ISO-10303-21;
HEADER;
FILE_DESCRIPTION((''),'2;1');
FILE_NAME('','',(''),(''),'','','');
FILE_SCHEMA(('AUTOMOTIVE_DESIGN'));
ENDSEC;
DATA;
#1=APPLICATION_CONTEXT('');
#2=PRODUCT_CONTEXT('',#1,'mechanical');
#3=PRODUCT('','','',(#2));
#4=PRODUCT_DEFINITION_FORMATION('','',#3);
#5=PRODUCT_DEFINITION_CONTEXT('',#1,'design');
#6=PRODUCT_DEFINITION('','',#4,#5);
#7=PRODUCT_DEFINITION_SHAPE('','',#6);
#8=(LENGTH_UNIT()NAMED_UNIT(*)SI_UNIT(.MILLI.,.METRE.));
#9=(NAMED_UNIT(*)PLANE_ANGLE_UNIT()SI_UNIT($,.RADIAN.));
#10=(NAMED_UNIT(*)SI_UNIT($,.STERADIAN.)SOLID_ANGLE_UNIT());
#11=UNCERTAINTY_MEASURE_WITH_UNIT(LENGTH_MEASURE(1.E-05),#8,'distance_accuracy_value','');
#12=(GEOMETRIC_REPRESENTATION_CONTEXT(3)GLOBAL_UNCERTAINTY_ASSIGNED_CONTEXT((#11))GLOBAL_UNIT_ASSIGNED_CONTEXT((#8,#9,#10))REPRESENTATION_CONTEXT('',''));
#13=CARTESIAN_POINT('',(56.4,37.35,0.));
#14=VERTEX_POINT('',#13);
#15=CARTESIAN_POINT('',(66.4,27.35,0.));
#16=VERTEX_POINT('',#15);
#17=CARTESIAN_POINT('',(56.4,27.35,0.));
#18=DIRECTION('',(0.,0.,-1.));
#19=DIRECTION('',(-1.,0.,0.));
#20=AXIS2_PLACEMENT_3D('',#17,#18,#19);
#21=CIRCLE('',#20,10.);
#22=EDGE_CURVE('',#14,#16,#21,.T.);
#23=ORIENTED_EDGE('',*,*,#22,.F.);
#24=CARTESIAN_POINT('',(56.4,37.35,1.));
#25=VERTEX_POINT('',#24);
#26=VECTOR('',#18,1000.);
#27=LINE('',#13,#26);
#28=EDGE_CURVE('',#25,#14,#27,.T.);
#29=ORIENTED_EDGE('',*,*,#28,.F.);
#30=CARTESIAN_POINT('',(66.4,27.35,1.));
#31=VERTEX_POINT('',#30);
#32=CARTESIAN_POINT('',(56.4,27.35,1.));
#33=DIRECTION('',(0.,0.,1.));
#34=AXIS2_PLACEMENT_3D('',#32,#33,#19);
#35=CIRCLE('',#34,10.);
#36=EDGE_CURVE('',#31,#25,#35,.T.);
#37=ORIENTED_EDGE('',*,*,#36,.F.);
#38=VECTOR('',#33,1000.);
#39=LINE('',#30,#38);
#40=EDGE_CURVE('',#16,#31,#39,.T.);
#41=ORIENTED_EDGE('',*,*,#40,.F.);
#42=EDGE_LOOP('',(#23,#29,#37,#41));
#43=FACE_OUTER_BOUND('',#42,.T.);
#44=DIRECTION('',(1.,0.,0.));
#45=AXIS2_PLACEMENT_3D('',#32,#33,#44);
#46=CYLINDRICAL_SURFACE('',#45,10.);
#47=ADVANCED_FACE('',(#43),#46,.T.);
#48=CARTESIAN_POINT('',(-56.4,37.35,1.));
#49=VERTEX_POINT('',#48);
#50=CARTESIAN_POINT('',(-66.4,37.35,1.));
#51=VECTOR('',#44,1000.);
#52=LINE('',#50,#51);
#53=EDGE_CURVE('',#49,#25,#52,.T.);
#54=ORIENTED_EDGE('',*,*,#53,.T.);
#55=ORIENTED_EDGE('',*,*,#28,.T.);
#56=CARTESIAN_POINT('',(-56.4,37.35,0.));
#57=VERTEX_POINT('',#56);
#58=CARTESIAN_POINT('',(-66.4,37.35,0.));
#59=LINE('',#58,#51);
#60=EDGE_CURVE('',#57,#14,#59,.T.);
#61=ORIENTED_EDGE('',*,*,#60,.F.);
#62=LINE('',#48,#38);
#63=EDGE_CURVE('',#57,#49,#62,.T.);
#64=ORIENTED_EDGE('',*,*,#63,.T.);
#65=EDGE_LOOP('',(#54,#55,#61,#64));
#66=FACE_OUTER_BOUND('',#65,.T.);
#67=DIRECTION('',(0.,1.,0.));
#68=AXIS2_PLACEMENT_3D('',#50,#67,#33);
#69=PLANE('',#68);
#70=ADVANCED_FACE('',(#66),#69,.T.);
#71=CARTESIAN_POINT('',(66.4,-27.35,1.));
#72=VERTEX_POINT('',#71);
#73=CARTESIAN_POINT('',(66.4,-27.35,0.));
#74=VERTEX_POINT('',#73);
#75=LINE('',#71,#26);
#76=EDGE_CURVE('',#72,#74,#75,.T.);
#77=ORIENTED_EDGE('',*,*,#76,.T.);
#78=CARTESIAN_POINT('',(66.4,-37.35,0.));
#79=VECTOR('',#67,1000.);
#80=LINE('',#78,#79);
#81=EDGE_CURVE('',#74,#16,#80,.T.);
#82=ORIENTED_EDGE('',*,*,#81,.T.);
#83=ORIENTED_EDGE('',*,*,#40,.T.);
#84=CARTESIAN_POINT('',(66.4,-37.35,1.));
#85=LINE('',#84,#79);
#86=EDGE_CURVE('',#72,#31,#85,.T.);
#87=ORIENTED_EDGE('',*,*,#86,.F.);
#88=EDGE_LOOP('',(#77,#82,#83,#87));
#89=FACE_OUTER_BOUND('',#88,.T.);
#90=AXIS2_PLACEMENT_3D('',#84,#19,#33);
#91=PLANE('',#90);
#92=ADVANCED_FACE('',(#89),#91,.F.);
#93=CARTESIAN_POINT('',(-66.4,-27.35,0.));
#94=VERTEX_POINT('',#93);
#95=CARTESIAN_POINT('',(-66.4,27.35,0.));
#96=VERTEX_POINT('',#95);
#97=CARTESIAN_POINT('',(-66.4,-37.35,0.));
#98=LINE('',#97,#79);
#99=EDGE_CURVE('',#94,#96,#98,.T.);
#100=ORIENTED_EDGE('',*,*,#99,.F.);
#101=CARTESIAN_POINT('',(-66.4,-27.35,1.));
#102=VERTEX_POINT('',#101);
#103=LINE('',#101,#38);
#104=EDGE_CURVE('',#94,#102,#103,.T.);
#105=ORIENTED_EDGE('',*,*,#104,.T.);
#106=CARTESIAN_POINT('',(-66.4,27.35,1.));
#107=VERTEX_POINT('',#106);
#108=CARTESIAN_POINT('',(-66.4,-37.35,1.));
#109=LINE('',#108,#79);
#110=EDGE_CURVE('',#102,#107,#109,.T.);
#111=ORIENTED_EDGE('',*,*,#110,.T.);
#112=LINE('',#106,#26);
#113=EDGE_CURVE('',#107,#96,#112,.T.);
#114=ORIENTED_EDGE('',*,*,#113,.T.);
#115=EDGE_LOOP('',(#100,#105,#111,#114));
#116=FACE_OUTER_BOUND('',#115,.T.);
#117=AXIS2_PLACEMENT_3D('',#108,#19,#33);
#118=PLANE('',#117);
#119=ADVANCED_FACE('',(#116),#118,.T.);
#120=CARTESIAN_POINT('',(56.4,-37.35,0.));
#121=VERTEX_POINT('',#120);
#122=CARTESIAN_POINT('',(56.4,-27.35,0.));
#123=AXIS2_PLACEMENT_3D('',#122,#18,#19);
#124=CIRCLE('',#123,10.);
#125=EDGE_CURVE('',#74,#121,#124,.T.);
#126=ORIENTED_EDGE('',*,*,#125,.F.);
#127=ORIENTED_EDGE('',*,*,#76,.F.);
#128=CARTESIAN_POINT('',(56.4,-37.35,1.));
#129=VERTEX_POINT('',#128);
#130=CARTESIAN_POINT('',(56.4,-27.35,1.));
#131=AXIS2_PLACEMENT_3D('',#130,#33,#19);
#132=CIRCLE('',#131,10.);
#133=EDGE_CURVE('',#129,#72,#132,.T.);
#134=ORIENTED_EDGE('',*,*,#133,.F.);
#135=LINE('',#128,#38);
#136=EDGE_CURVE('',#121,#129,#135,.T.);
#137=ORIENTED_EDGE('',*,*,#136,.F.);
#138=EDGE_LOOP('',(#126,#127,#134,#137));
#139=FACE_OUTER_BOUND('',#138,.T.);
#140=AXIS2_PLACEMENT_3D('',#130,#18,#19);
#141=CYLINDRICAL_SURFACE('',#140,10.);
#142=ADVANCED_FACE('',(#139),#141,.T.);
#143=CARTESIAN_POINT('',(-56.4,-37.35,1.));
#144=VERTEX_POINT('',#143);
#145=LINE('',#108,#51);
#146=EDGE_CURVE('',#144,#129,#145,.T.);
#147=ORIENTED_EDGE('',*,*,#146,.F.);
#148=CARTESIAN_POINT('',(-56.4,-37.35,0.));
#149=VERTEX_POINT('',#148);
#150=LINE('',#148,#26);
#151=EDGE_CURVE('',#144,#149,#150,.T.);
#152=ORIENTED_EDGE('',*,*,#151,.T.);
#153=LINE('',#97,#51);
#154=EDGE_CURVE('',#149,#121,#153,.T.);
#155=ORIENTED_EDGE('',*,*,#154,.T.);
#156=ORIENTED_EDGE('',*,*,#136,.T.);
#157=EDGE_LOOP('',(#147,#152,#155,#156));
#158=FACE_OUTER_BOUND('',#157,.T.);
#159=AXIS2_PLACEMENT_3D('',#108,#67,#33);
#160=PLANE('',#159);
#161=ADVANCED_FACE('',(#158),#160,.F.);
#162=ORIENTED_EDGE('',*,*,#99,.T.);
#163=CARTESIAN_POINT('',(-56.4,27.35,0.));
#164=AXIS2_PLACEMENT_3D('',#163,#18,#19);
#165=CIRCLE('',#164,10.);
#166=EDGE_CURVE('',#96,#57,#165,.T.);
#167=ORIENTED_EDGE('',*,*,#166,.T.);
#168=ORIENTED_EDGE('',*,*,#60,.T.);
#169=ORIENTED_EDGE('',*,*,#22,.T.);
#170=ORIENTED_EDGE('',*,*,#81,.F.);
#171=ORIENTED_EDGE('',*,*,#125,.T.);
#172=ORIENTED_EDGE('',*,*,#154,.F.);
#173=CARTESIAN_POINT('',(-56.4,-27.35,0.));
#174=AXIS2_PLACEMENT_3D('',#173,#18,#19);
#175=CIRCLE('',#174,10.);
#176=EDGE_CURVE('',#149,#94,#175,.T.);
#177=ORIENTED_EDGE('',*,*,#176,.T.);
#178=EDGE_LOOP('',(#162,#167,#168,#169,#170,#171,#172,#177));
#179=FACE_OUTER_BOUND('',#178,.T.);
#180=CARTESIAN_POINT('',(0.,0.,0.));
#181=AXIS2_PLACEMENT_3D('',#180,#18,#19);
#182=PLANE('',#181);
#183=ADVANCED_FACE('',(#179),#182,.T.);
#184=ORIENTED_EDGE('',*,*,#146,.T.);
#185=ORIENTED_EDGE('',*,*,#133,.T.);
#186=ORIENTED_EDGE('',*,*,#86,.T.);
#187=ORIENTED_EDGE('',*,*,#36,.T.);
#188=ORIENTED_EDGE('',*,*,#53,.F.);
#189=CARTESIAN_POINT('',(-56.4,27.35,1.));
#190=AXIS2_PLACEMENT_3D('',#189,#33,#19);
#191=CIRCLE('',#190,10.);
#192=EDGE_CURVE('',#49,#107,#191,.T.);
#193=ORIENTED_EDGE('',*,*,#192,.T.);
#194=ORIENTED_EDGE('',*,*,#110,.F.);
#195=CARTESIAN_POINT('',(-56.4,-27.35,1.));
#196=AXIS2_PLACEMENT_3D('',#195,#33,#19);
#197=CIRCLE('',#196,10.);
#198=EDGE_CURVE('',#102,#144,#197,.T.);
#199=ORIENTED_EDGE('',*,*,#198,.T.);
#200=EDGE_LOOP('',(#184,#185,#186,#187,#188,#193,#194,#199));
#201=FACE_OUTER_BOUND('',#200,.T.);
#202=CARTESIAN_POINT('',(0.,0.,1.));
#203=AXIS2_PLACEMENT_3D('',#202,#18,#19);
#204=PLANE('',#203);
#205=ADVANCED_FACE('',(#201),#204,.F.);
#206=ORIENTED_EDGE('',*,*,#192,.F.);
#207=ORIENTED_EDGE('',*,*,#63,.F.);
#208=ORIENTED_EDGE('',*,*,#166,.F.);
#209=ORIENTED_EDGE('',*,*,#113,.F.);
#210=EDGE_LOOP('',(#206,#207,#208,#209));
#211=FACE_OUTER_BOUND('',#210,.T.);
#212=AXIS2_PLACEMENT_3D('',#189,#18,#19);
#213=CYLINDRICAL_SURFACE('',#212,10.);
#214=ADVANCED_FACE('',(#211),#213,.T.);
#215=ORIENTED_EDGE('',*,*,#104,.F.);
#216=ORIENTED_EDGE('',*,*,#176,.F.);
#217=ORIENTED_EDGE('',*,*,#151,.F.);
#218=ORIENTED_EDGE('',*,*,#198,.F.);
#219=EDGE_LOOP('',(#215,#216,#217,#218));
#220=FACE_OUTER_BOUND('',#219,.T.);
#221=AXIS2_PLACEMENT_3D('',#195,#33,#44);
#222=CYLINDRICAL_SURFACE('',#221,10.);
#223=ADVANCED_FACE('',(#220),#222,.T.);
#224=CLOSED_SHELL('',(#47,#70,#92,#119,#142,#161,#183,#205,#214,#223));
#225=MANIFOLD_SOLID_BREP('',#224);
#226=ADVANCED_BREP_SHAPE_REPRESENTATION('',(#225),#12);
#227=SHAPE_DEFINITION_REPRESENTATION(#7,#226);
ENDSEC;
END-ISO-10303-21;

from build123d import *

# Parameters (mm, degrees)
SKETCH1_W           = 132.8
SKETCH1_H           = 74.7
BOSS_EXTRUDE1_DEPTH = 1
FILLET1_R           = 10


with BuildPart() as part:
    # Sketch1 → Boss-Extrude1 (new body)
    with BuildSketch(Plane.XY):
        Rectangle(SKETCH1_W, SKETCH1_H)
    extrude(amount=BOSS_EXTRUDE1_DEPTH)

    # Fillet1
    fillet1_edges = [part.edges().sort_by_distance(p)[0] for p in [
        (-66.4, -37.35, 0.5),
        (66.4, -37.35, 0.5),
        (66.4, 37.35, 0.5),
        (-66.4, 37.35, 0.5),
    ]]
    fillet(fillet1_edges, radius=FILLET1_R)


solid = part.part
